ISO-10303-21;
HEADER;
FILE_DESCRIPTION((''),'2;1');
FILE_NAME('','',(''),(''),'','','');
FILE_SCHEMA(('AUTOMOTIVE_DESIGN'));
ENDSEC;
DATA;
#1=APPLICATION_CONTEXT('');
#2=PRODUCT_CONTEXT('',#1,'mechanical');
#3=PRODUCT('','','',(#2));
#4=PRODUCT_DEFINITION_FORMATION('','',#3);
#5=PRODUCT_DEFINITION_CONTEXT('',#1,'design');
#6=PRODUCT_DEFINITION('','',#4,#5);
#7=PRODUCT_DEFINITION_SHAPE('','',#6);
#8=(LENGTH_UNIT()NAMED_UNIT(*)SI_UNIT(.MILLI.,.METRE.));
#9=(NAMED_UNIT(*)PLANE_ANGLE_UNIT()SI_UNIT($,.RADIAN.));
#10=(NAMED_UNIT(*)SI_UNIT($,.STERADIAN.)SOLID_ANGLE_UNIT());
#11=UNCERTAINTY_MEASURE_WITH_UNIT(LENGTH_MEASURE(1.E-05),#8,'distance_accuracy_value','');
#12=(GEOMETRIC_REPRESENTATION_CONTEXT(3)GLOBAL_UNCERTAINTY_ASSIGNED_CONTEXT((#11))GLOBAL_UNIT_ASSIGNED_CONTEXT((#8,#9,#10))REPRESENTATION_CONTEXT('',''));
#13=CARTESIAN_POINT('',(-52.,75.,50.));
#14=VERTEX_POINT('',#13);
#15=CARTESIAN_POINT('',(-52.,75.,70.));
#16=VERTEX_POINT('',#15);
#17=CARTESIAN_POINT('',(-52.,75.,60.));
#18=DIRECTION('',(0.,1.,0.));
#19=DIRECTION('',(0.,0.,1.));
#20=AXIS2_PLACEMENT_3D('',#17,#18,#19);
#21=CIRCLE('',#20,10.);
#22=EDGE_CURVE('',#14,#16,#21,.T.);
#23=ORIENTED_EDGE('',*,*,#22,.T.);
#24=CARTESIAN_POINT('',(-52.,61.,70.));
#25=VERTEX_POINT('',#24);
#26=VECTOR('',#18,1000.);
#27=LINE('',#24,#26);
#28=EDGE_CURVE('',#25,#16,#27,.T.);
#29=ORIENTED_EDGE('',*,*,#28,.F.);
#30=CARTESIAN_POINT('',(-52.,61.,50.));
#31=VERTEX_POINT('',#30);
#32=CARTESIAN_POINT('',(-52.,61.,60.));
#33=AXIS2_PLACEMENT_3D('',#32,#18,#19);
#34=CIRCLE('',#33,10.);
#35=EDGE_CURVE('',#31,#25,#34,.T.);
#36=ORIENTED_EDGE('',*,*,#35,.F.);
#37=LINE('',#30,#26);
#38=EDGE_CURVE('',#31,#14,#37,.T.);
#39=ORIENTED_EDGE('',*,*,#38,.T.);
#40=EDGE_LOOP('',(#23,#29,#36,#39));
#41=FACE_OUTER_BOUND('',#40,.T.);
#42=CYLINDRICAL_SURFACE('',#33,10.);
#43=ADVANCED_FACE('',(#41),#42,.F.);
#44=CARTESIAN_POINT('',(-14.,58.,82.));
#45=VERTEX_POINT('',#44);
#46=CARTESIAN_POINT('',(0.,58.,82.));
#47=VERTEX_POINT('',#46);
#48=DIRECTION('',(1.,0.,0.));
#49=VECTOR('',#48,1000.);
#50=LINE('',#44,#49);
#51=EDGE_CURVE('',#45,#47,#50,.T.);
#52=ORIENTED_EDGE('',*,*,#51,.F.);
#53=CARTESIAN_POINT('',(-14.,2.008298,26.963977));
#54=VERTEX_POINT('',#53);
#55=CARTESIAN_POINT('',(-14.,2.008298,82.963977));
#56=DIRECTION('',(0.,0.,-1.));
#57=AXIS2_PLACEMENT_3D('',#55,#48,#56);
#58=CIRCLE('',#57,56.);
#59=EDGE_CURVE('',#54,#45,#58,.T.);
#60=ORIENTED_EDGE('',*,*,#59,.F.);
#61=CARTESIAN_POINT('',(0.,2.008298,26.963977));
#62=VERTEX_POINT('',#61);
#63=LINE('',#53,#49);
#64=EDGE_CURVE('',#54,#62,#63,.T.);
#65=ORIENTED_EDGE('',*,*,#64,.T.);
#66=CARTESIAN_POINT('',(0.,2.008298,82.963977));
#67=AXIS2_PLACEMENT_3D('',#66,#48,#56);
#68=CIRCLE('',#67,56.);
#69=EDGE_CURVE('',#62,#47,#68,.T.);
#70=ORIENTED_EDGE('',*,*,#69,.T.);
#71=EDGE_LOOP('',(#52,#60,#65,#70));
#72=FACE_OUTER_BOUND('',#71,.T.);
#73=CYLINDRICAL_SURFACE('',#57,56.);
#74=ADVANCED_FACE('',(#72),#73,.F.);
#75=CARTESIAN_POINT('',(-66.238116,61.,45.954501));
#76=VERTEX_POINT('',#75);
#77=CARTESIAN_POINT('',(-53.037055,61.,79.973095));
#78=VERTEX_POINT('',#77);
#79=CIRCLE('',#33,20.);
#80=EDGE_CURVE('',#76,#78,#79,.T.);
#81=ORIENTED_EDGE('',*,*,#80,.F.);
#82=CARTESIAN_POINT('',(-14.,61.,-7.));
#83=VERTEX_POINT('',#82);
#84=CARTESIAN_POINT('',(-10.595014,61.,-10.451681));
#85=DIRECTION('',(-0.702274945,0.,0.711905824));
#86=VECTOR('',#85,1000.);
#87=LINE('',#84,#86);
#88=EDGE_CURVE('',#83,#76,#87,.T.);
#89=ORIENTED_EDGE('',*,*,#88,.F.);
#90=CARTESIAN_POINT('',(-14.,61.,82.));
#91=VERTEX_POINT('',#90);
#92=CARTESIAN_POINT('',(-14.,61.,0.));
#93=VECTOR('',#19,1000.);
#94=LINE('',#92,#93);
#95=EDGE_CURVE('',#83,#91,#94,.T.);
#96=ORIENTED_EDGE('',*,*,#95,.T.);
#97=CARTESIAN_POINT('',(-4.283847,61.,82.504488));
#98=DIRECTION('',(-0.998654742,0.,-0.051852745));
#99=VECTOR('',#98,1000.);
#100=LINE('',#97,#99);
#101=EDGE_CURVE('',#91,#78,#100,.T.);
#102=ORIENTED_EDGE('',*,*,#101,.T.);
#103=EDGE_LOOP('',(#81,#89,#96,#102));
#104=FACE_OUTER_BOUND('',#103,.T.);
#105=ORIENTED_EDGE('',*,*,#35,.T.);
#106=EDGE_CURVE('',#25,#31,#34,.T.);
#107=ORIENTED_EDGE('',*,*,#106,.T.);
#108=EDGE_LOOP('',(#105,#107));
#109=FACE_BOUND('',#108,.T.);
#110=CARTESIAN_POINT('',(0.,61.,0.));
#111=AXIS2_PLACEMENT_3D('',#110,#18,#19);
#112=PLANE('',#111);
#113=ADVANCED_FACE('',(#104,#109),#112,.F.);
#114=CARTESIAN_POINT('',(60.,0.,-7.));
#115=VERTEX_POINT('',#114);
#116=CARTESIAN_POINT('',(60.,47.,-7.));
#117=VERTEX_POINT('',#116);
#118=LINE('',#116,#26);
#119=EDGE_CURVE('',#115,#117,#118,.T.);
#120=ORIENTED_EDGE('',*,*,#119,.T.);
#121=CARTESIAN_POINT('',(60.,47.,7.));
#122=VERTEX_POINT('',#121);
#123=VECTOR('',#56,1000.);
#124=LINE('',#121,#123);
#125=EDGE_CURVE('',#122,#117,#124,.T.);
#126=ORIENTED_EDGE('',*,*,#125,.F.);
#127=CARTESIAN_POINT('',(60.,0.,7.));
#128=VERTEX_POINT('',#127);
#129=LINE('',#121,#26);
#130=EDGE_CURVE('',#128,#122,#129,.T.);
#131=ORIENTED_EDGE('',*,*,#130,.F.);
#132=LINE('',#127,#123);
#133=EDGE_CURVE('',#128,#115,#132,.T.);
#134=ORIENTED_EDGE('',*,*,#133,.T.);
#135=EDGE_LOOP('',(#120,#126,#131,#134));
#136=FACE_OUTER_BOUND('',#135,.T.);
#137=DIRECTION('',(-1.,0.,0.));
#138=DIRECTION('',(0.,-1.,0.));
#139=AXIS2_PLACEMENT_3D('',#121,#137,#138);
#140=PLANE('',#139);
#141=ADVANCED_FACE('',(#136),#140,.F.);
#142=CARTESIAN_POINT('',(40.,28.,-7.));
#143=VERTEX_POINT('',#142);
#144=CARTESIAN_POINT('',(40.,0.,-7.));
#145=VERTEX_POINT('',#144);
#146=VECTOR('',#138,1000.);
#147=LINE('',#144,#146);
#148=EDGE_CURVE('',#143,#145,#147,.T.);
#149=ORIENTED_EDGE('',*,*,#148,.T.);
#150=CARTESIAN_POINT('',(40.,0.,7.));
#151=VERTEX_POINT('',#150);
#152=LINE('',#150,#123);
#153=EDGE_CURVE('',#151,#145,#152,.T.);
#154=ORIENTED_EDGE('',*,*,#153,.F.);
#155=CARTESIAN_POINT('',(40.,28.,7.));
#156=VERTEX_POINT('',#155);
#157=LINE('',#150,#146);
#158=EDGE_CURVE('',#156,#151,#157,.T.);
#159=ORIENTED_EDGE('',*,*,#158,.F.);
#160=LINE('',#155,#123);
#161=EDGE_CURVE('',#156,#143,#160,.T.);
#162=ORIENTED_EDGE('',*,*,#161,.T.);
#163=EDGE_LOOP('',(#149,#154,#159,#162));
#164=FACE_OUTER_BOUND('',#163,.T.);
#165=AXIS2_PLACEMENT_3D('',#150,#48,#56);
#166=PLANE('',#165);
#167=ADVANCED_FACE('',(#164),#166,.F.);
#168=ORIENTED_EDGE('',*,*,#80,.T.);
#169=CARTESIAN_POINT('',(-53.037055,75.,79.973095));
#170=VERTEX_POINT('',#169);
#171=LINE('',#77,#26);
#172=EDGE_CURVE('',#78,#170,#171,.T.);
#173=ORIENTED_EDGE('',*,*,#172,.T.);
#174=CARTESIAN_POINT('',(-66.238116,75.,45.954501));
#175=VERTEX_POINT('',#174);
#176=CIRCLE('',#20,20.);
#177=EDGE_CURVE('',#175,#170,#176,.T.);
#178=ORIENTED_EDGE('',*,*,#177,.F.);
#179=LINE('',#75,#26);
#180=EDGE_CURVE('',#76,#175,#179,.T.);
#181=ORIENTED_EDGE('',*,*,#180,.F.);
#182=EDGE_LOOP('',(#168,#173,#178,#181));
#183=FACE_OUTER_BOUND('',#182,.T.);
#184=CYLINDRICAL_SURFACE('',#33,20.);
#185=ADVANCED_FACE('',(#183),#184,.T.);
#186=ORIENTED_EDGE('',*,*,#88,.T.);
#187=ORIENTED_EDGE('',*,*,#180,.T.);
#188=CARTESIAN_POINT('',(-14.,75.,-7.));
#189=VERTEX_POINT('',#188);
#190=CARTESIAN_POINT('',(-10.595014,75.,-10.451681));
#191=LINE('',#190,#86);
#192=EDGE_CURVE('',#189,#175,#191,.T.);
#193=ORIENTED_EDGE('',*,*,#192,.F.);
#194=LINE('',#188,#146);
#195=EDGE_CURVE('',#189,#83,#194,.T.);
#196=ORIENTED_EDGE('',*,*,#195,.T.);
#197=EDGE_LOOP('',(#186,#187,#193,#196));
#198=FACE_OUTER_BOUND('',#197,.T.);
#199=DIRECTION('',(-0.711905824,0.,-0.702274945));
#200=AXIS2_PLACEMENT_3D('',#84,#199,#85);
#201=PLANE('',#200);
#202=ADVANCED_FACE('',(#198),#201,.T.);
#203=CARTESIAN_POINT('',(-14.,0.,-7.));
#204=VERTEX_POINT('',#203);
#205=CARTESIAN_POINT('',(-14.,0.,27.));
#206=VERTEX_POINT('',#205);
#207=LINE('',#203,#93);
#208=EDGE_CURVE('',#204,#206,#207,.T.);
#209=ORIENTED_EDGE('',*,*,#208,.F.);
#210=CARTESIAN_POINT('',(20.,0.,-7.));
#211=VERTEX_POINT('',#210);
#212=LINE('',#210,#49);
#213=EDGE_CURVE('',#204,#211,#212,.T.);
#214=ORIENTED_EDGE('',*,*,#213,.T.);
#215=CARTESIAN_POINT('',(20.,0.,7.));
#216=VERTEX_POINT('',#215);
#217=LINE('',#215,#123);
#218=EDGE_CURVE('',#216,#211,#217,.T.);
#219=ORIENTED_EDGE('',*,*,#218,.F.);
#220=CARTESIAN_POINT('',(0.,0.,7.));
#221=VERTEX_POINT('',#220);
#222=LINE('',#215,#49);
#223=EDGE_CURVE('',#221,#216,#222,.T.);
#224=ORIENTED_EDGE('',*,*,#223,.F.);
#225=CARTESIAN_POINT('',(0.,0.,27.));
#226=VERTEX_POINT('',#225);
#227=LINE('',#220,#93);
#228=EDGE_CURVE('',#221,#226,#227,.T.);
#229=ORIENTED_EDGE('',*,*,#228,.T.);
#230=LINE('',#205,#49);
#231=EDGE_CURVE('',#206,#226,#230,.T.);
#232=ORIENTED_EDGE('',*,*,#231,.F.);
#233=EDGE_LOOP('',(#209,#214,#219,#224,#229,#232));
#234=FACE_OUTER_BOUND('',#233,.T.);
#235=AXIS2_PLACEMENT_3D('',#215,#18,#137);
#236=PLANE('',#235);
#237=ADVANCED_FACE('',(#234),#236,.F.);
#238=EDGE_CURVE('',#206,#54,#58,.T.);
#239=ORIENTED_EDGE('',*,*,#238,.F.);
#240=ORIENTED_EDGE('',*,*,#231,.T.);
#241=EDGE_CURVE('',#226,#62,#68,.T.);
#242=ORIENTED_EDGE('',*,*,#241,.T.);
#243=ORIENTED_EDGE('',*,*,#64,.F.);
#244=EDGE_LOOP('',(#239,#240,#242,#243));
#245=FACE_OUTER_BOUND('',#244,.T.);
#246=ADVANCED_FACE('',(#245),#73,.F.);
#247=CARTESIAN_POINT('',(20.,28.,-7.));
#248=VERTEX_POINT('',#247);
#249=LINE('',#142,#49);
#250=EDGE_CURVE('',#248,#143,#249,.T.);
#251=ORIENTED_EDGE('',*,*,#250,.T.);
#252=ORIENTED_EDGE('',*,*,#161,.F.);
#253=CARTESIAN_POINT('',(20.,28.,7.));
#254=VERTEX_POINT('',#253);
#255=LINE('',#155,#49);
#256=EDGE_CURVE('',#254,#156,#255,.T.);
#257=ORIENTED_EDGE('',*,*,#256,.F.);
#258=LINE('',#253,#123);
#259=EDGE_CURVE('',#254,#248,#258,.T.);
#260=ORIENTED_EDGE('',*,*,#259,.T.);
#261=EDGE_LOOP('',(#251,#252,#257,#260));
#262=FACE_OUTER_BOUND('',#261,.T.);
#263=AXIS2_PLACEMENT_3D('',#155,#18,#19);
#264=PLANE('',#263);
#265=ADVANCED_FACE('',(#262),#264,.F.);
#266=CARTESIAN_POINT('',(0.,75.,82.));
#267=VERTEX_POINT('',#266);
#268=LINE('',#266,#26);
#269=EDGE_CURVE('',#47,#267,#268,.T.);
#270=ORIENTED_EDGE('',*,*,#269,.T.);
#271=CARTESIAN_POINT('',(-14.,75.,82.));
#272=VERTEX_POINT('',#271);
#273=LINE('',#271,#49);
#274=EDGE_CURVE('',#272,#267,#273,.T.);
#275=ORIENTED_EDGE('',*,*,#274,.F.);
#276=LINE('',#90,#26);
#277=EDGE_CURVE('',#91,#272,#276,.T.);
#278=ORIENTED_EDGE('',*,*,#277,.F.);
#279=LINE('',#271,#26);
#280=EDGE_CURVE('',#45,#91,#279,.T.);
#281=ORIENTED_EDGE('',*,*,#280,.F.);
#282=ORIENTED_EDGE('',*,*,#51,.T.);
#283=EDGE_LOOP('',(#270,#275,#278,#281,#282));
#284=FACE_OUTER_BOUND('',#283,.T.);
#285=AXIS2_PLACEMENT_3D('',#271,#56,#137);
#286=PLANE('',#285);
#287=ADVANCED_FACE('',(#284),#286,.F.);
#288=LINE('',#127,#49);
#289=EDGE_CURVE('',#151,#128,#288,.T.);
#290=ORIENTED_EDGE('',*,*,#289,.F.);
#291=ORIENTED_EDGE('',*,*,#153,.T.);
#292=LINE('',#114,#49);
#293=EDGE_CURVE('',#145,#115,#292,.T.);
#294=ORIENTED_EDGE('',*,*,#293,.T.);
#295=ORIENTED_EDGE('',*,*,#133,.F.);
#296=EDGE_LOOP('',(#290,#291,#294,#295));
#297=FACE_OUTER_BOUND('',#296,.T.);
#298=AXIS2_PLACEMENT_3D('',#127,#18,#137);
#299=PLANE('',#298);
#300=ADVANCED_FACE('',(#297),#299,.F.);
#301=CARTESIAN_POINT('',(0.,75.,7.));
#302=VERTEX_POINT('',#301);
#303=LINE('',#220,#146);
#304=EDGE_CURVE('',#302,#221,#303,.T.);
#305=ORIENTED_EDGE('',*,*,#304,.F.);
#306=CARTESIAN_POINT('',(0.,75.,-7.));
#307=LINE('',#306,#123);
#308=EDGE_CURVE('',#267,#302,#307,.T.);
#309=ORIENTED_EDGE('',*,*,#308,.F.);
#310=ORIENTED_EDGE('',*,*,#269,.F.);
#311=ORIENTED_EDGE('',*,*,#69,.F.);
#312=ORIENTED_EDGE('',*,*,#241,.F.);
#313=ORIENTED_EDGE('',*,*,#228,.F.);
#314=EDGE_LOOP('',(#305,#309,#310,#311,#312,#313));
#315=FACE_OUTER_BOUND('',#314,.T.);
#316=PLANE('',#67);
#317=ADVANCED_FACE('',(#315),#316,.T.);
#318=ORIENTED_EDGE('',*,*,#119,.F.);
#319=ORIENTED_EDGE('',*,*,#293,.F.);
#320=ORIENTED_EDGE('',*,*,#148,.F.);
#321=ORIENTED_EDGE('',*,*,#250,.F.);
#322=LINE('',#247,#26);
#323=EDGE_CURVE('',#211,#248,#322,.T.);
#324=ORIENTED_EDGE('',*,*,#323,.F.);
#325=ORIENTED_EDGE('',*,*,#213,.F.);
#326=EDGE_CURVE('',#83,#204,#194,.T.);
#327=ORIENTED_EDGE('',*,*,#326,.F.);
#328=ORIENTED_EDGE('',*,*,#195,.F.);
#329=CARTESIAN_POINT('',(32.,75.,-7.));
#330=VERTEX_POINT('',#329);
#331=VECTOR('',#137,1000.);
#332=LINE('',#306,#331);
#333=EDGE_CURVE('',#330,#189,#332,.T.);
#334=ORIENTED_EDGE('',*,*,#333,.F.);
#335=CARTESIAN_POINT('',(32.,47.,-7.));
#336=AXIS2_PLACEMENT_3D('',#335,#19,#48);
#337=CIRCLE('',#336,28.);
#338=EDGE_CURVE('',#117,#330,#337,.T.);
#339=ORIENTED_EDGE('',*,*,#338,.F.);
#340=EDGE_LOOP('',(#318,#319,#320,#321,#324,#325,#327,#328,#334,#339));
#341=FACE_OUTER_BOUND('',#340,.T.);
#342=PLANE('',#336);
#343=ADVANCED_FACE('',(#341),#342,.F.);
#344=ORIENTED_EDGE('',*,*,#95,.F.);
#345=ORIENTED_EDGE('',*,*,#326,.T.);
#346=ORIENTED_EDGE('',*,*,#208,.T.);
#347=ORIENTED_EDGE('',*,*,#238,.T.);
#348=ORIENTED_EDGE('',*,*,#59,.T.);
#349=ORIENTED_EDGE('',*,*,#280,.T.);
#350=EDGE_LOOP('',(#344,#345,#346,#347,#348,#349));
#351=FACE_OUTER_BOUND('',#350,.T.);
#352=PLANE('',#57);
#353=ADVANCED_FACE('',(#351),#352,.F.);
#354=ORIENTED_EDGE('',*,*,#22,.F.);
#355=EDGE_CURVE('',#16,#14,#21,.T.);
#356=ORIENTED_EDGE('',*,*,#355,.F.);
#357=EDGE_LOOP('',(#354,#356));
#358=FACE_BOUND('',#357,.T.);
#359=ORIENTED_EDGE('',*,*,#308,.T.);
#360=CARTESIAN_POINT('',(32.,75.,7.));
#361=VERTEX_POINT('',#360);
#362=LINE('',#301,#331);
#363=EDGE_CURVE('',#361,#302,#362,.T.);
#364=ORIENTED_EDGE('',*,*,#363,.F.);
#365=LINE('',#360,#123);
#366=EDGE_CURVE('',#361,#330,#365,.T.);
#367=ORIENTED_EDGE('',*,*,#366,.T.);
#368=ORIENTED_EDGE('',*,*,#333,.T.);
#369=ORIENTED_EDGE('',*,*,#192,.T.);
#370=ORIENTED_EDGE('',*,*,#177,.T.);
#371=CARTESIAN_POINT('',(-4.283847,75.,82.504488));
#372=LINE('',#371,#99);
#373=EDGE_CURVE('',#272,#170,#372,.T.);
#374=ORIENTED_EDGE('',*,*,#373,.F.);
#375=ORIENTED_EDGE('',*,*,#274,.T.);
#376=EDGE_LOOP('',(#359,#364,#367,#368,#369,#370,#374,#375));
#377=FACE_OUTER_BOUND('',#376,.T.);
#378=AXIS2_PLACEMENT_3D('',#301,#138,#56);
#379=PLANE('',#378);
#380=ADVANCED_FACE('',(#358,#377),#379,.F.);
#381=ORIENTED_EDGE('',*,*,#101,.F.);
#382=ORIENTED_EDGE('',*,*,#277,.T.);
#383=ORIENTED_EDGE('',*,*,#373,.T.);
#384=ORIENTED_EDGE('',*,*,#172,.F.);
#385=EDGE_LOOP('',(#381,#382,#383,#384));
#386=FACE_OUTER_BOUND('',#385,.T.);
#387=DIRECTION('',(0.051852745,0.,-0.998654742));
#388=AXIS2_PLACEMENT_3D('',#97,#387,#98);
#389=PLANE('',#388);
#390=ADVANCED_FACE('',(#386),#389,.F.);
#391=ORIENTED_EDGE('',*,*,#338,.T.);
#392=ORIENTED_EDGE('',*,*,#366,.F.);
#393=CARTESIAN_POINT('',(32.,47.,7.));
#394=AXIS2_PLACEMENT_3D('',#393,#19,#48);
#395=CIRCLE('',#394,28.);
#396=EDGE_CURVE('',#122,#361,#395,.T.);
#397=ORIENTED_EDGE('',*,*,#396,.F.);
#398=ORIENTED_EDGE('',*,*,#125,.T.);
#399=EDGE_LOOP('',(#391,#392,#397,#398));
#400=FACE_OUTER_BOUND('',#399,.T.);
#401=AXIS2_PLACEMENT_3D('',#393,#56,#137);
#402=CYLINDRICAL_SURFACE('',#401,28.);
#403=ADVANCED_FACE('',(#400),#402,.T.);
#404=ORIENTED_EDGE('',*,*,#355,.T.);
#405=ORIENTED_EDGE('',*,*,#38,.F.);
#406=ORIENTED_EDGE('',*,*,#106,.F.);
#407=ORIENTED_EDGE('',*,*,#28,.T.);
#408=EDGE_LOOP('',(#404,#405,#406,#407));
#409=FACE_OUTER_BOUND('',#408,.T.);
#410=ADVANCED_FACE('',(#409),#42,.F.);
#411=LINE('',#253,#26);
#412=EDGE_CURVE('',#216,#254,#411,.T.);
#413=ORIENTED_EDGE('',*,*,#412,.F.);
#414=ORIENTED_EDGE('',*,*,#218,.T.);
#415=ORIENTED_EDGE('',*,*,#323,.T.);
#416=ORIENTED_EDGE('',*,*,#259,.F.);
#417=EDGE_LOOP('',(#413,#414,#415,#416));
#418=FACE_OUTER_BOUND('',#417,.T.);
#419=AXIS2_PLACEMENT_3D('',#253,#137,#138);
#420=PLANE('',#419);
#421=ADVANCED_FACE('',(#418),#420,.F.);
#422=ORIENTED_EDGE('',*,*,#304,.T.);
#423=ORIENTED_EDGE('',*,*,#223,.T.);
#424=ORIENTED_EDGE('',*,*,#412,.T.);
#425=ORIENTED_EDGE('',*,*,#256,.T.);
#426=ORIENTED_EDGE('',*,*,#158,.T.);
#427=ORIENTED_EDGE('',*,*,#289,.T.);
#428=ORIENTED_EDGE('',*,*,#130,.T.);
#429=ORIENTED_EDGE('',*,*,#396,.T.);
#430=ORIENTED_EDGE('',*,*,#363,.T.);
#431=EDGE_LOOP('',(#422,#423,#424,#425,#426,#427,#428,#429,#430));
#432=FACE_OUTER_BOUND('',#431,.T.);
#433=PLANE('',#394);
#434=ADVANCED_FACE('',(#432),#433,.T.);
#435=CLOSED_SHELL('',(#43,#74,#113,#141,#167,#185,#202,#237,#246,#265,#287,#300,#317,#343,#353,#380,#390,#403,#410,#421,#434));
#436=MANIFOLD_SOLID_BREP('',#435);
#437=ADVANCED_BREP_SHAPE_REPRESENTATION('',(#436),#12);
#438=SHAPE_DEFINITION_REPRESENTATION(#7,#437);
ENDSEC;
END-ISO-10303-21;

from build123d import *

# Parameters (mm, degrees)
BASE_PLATE_14MM_DEPTH        = 7
SIDE_PLATE_14MM_DEPTH        = 14
SLOTTED_END_PLATE_PROFILE_R  = 10
SLOTTED_END_PLATE_14MM_DEPTH = 14


with BuildPart() as part:
    # Base Plate Profile → Base Plate 14mm (new, symmetric)
    with BuildSketch(Plane.XY):
        with BuildLine():
            Line((0, 0), (0, 75))
            Line((0, 75), (32, 75))
            ThreePointArc((32, 75), (51.798989873, 66.798989873), (60, 47))
            Line((60, 47), (60, 0))
            Line((60, 0), (40, 0))
            Line((40, 0), (40, 28))
            Line((40, 28), (20, 28))
            Line((20, 28), (20, 0))
            Line((20, 0), (0, 0))
        make_face()
    extrude(amount=BASE_PLATE_14MM_DEPTH, both=True)

    # Side Plate Profile → Side Plate 14mm (add)
    with BuildSketch(Plane.ZY):
        with BuildLine():
            Line((-7, 75), (82, 75))
            Line((82, 75), (82, 58))
            ThreePointArc((82, 58), (42.329041508, 40.541426156), (27, 0))
            Line((27, 0), (7, 0))
            Line((7, 0), (-7, 0))
            Line((-7, 0), (-7, 75))
        make_face()
    extrude(amount=SIDE_PLATE_14MM_DEPTH)

    # Slotted End Plate Profile → Slotted End Plate 14mm (add)
    with BuildSketch(Plane(origin=(0, 75, 0), x_dir=(1, 0, 0), z_dir=(0, 1, 0))):
        with BuildLine():
            Line((-53.037054902, -79.973094831), (-14, -82))
            Line((-14, -82), (-14, 7))
            Line((-14, 7), (-66.238116475, -45.954501104))
            ThreePointArc((-66.238116475, -45.954501104), (-70.645345128, -67.23540635), (-53.037054902, -79.973094831))
        make_face()
        with Locations(Location((-52, -60, 0), (0, 0, 270))):
            Circle(SLOTTED_END_PLATE_PROFILE_R, mode=Mode.SUBTRACT)
    extrude(amount=-SLOTTED_END_PLATE_14MM_DEPTH)


solid = part.part
